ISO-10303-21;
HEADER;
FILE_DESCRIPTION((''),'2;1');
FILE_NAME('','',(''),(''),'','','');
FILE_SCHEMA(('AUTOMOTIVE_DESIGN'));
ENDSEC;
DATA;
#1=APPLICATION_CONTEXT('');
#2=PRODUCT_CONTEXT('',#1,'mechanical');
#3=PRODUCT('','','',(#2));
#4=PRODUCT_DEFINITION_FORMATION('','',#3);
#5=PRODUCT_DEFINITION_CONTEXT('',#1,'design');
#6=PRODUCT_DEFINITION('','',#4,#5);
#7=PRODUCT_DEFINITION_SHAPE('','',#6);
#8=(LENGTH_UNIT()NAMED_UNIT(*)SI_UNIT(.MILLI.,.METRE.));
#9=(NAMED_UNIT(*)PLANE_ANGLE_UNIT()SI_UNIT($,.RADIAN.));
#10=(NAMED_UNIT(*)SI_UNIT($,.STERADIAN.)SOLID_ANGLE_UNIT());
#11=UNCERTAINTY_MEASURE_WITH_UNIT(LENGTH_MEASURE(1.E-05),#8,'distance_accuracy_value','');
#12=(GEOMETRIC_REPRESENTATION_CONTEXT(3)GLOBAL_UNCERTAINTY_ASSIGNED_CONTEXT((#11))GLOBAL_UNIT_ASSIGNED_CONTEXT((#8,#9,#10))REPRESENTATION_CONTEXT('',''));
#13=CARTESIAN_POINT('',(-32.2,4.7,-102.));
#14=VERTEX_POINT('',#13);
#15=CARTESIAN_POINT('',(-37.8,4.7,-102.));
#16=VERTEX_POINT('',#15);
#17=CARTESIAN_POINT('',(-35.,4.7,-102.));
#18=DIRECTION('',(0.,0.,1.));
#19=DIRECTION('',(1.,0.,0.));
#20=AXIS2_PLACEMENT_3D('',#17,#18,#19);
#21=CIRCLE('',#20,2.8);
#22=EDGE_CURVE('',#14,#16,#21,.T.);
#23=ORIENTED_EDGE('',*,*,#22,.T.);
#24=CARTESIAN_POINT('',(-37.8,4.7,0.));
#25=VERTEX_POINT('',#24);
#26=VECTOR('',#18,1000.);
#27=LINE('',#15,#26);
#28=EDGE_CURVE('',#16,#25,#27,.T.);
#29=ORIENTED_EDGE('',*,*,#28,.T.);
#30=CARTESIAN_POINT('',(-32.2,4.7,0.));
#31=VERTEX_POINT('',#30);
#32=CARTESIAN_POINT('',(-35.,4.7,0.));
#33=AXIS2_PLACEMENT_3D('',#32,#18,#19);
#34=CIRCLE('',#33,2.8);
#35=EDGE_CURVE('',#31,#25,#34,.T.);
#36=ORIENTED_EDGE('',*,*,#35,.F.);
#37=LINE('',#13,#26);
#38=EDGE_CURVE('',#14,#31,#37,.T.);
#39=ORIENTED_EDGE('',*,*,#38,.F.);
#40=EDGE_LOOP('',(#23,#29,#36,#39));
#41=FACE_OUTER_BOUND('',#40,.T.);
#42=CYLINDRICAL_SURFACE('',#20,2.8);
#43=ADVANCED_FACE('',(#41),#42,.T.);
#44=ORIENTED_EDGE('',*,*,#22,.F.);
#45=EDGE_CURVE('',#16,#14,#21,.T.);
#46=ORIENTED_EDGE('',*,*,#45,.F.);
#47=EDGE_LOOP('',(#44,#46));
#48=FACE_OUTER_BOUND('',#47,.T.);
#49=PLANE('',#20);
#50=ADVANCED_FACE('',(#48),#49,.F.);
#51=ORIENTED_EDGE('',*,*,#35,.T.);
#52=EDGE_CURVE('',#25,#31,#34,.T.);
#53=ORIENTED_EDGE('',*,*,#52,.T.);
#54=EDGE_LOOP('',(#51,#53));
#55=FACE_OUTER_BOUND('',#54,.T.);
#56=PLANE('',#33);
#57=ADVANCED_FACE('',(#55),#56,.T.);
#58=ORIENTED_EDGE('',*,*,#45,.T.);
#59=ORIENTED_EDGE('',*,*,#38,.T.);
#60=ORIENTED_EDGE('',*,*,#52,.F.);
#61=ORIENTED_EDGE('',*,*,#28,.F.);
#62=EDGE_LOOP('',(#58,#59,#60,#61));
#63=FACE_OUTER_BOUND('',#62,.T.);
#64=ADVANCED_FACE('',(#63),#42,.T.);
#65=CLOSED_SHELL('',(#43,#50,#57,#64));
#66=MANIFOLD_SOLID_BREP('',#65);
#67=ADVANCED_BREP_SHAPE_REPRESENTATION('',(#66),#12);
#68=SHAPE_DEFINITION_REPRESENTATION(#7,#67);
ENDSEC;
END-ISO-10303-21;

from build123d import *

# Parameters (mm, degrees)
SKETCH1_R           = 2.8
BOSS_EXTRUDE1_DEPTH = 102


with BuildPart() as part:
    # Sketch1 → Boss-Extrude1 (new body)
    with BuildSketch(Plane.XY):
        with Locations((-35, 4.7)):
            Circle(SKETCH1_R)
    extrude(amount=-BOSS_EXTRUDE1_DEPTH)


solid = part.part
